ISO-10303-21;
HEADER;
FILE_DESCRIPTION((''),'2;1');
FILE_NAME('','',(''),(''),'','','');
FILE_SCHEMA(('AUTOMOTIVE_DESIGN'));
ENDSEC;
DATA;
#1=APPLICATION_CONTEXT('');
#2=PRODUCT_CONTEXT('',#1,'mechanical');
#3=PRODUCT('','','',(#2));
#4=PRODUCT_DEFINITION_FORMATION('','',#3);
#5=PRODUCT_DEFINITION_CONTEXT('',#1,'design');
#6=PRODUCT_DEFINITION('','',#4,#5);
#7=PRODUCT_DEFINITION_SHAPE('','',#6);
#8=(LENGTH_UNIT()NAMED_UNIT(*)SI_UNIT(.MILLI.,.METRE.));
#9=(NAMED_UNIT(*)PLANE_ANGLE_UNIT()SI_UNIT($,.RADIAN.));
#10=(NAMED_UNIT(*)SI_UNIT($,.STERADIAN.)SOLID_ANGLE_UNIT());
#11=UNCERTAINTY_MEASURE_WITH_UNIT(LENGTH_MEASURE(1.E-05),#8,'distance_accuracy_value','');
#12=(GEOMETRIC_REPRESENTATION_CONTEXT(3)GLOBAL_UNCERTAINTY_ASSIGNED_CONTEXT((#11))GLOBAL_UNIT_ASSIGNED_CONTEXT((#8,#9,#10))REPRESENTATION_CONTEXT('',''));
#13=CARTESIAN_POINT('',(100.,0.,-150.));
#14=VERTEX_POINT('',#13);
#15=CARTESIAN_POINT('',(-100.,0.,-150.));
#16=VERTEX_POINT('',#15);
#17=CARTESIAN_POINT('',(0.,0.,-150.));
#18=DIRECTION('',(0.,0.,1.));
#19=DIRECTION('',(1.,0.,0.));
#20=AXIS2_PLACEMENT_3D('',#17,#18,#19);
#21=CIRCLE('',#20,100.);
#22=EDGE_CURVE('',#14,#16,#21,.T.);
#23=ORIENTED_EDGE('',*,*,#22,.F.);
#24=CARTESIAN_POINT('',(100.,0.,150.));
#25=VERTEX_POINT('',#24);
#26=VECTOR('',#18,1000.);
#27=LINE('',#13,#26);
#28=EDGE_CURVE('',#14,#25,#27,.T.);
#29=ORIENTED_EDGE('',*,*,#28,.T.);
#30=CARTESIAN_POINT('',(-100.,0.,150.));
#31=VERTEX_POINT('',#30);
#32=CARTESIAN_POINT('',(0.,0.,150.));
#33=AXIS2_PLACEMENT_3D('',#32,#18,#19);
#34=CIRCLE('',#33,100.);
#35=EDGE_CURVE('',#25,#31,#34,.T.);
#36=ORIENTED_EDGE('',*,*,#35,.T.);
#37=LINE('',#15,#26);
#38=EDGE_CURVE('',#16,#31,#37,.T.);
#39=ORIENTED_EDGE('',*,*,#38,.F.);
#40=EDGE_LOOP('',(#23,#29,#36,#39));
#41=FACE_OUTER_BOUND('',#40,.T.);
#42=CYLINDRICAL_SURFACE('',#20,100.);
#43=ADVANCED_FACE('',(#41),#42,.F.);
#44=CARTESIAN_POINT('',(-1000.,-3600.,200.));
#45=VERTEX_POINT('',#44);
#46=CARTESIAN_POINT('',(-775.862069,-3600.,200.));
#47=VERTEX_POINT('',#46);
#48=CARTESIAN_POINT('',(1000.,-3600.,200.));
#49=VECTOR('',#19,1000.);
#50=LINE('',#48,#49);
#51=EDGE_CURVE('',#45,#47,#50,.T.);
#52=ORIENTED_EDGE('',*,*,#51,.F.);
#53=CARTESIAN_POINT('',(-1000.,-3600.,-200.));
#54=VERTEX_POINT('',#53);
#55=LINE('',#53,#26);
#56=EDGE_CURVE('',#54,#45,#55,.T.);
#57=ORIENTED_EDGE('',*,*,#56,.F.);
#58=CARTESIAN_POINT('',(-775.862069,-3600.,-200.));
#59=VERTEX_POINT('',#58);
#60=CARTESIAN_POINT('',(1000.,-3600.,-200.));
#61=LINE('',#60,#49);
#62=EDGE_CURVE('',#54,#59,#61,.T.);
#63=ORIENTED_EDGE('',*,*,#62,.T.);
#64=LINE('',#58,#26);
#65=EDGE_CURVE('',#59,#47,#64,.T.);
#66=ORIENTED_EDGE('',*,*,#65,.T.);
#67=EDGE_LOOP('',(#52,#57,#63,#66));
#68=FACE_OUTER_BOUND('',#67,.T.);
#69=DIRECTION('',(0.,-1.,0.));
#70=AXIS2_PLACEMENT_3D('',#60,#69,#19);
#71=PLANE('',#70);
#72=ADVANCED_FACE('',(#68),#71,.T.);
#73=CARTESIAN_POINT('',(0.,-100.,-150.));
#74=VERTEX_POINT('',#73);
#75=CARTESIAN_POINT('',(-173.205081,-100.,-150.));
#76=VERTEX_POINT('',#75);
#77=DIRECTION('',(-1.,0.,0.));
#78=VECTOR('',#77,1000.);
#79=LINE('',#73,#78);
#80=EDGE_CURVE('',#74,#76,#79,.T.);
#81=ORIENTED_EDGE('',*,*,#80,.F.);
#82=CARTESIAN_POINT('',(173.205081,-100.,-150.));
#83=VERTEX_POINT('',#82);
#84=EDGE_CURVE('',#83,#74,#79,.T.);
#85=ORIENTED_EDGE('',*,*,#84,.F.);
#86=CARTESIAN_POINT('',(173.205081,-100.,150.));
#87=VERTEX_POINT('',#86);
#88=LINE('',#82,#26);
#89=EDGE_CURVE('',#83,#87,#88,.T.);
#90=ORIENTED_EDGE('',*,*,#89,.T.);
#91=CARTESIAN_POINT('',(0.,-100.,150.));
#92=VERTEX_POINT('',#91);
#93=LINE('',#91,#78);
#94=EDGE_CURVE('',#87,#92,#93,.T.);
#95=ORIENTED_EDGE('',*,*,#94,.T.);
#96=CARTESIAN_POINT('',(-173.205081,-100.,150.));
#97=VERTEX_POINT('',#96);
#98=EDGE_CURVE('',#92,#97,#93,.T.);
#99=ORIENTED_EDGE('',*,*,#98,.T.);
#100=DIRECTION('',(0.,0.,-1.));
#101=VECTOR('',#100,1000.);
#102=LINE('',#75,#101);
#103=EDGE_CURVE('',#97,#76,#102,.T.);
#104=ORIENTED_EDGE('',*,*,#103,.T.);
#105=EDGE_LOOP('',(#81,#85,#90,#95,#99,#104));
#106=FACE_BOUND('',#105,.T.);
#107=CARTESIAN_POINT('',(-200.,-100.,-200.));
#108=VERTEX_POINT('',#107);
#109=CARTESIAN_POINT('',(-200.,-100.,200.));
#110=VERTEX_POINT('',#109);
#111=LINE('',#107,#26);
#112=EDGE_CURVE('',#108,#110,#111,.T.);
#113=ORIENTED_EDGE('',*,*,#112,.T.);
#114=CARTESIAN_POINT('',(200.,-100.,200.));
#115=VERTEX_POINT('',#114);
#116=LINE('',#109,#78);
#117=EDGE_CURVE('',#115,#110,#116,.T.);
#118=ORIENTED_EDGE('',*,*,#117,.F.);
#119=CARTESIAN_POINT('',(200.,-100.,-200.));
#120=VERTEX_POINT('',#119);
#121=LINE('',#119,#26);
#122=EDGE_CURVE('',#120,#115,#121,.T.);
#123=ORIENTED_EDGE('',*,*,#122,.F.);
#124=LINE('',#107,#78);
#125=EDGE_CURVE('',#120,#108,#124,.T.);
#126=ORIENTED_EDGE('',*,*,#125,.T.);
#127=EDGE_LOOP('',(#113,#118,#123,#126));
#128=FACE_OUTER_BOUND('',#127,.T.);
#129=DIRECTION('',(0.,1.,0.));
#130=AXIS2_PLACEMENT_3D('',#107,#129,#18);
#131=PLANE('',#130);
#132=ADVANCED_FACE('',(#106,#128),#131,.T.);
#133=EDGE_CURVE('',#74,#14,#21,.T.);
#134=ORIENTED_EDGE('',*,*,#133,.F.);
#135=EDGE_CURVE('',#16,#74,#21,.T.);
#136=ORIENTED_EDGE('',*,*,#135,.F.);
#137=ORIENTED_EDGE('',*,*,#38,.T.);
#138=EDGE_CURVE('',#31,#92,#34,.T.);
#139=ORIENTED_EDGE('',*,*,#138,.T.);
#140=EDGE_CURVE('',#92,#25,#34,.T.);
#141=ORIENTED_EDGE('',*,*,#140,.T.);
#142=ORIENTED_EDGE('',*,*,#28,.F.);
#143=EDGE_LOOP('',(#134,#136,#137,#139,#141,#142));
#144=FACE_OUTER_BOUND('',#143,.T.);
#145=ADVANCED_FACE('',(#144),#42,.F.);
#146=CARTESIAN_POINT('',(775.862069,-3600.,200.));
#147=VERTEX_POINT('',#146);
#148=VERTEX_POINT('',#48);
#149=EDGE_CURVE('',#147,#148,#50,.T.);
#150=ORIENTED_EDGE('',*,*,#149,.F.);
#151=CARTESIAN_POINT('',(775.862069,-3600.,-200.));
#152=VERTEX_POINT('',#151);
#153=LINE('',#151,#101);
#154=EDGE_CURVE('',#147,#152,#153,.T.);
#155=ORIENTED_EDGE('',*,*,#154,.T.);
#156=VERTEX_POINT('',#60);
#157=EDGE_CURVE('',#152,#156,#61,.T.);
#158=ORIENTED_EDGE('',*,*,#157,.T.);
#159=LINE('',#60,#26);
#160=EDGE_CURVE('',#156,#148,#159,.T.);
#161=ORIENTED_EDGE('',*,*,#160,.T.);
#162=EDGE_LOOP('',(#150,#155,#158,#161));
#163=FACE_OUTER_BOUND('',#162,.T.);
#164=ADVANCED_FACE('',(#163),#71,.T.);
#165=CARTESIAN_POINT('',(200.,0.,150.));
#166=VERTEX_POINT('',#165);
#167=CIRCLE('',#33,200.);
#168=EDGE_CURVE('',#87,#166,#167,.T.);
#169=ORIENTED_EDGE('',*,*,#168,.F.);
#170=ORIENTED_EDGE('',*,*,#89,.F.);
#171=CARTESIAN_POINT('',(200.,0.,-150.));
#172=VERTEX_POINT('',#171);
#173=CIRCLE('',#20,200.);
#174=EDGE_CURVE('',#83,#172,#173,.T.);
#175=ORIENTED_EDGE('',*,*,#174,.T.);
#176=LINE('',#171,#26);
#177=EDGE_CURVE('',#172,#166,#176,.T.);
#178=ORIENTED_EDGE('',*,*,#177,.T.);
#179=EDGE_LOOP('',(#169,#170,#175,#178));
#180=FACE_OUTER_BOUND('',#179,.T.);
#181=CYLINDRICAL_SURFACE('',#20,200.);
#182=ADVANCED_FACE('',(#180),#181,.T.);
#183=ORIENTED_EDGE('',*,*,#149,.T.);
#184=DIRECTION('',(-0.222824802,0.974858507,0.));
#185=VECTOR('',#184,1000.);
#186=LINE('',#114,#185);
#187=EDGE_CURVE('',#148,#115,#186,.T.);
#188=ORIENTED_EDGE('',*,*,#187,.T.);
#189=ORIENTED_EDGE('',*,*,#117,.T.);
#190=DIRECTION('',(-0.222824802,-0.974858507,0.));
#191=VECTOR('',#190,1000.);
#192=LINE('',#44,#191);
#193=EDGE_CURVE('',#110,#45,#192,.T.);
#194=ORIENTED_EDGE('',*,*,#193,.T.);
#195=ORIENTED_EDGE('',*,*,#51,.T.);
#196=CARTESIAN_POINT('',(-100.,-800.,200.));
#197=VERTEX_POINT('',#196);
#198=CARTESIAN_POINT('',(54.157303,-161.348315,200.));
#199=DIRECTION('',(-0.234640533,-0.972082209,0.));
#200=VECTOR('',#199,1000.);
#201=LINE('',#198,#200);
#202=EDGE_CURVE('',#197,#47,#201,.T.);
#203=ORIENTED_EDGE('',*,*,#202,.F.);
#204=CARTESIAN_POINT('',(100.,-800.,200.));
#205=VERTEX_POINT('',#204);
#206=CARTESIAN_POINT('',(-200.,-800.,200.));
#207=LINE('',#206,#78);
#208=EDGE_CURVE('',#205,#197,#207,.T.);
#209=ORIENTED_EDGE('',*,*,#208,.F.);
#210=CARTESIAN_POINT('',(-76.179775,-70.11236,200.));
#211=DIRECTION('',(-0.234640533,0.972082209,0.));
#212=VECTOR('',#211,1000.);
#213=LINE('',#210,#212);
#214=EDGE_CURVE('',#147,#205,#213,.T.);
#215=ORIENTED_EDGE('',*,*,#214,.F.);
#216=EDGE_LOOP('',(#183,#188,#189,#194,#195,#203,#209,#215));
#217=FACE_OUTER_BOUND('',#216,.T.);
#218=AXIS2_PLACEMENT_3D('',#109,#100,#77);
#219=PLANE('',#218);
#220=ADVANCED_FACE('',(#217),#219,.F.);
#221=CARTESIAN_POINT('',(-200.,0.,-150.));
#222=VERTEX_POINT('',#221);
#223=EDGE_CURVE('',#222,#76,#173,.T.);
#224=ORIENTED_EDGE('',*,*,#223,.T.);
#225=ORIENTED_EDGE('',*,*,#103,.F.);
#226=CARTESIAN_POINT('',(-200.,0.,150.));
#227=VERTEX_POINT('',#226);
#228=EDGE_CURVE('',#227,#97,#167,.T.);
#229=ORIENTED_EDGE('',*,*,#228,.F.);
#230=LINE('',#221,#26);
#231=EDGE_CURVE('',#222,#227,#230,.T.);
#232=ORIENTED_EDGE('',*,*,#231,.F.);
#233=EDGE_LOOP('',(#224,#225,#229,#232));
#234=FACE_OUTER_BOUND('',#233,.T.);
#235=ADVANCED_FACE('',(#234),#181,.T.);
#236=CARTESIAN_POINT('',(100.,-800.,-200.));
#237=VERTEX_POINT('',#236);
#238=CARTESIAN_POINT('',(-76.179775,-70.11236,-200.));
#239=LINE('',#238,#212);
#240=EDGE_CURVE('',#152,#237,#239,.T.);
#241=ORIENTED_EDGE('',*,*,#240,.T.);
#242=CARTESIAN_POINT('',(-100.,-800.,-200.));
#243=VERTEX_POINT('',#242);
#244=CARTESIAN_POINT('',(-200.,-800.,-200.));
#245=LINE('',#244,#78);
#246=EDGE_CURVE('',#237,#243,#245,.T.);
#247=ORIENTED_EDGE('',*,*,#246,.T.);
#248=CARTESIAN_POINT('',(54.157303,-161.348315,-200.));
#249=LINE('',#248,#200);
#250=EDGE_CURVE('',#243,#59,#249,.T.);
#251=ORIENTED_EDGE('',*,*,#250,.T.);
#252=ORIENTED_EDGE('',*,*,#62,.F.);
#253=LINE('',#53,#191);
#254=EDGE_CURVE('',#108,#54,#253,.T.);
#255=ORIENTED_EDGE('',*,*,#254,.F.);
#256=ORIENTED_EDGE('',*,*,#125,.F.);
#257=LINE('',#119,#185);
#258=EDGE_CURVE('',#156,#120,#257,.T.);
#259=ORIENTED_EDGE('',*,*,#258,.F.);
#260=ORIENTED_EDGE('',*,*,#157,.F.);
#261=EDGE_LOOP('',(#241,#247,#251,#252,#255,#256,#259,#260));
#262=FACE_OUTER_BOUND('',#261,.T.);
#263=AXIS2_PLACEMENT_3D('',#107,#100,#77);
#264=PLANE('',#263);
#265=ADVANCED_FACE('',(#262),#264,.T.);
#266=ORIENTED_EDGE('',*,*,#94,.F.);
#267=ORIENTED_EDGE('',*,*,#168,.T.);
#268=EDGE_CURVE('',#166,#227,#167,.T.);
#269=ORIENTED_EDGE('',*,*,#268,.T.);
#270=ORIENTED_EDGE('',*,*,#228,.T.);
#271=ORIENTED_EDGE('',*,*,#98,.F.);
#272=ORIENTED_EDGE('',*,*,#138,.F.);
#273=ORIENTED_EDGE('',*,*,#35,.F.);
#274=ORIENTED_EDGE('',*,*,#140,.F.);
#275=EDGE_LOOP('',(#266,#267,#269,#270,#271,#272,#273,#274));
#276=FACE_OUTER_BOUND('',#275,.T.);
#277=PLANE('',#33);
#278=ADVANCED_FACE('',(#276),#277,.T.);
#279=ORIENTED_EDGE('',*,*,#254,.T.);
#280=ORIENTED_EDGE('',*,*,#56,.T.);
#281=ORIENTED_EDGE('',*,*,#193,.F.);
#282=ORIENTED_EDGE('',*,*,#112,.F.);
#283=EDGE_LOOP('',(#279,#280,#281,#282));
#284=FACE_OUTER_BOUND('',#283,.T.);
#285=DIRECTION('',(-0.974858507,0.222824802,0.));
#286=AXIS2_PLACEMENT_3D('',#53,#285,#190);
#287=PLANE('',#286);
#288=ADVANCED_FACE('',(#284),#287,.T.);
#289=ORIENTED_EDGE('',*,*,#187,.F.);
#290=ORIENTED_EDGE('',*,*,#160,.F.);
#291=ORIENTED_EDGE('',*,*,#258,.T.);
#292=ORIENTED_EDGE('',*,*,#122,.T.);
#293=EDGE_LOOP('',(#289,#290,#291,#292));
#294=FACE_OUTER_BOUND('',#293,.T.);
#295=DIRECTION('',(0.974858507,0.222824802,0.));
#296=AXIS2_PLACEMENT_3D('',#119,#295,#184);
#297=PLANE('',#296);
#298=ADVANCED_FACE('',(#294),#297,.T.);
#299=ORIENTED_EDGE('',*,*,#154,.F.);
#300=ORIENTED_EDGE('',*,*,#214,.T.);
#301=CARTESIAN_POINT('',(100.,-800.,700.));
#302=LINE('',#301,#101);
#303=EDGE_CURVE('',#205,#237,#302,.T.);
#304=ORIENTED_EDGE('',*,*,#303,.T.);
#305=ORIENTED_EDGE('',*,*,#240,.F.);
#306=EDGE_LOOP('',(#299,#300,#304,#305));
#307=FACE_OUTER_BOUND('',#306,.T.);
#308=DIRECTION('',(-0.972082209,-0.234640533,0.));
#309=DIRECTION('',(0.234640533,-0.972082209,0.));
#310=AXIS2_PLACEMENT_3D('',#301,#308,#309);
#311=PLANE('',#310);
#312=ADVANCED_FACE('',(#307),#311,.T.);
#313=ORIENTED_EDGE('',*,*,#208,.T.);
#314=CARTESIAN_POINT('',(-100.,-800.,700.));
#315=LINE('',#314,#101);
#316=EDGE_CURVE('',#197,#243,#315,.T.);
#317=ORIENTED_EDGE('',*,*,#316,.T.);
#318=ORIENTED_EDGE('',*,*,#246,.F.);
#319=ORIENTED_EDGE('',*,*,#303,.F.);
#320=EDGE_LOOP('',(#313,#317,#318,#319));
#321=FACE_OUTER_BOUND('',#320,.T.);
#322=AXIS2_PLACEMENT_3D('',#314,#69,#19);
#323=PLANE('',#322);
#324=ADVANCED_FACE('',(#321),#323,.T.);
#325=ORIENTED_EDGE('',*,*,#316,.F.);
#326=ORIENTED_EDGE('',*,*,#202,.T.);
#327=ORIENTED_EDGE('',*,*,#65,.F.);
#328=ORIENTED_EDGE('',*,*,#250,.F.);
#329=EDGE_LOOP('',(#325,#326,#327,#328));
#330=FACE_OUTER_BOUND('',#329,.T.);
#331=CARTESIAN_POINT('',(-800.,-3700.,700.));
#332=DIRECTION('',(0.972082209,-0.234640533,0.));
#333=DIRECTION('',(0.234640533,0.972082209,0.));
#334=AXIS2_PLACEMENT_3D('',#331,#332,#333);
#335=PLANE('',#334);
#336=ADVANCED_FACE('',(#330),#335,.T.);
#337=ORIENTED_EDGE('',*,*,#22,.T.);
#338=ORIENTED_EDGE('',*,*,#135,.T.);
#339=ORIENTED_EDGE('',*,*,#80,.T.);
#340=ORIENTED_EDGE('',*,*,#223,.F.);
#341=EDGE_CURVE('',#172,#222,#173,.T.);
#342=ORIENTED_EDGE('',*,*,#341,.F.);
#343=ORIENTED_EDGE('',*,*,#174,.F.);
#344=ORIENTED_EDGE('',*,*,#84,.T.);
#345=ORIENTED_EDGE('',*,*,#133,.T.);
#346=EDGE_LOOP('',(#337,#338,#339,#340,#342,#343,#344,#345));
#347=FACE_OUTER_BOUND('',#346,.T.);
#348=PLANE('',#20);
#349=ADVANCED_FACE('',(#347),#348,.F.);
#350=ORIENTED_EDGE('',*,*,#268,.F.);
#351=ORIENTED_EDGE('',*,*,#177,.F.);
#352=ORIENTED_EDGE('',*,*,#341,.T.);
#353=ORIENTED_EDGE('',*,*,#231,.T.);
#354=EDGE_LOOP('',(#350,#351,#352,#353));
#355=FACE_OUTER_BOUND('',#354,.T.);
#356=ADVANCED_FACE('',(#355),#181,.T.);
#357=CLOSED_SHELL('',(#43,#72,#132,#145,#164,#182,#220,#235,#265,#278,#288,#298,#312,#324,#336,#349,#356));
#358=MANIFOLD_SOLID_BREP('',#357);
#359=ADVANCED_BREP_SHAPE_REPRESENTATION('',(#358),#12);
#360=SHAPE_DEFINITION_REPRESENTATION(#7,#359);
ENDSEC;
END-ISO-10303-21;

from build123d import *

# Parameters (mm, degrees)
BOSS_EXTRUDE1_DEPTH      = 150
BOSS_EXTRUDE1_DEPTH_BACK = 150
SKETCH1_R                = 200
SKETCH1_R_2              = 100
BOSS_EXTRUDE2_DEPTH      = 200
BOSS_EXTRUDE2_DEPTH_BACK = 200
CUT_EXTRUDE1_DEPTH       = 500
CUT_EXTRUDE1_DEPTH_BACK  = 500


with BuildPart() as part:
    # Sketch1 → Boss-Extrude1 (new, two sides: drawn at the far end of the back side and taken through both)
    with BuildSketch(Plane.XY.offset(-BOSS_EXTRUDE1_DEPTH_BACK)):
        Circle(SKETCH1_R)
        Circle(SKETCH1_R_2, mode=Mode.SUBTRACT)
    extrude(amount=BOSS_EXTRUDE1_DEPTH + BOSS_EXTRUDE1_DEPTH_BACK)

    # Sketch2 → Boss-Extrude2 (add, two sides: drawn at the far end of the back side and taken through both)
    with BuildSketch(Plane.XY.offset(-BOSS_EXTRUDE2_DEPTH_BACK)):
        Polygon((-200, -100), (200, -100), (1000, -3600), (-1000, -3600), align=None)
    extrude(amount=BOSS_EXTRUDE2_DEPTH + BOSS_EXTRUDE2_DEPTH_BACK)

    # Sketch3 → Cut-Extrude1 (cut, two sides: drawn at the far end of the back side and taken through both)
    with BuildSketch(Plane.XY.offset(200).offset(-CUT_EXTRUDE1_DEPTH_BACK)):
        Polygon((-100, -800), (100, -800), (800, -3700), (-800, -3700), align=None)
    extrude(amount=CUT_EXTRUDE1_DEPTH + CUT_EXTRUDE1_DEPTH_BACK, mode=Mode.SUBTRACT)


solid = part.part
